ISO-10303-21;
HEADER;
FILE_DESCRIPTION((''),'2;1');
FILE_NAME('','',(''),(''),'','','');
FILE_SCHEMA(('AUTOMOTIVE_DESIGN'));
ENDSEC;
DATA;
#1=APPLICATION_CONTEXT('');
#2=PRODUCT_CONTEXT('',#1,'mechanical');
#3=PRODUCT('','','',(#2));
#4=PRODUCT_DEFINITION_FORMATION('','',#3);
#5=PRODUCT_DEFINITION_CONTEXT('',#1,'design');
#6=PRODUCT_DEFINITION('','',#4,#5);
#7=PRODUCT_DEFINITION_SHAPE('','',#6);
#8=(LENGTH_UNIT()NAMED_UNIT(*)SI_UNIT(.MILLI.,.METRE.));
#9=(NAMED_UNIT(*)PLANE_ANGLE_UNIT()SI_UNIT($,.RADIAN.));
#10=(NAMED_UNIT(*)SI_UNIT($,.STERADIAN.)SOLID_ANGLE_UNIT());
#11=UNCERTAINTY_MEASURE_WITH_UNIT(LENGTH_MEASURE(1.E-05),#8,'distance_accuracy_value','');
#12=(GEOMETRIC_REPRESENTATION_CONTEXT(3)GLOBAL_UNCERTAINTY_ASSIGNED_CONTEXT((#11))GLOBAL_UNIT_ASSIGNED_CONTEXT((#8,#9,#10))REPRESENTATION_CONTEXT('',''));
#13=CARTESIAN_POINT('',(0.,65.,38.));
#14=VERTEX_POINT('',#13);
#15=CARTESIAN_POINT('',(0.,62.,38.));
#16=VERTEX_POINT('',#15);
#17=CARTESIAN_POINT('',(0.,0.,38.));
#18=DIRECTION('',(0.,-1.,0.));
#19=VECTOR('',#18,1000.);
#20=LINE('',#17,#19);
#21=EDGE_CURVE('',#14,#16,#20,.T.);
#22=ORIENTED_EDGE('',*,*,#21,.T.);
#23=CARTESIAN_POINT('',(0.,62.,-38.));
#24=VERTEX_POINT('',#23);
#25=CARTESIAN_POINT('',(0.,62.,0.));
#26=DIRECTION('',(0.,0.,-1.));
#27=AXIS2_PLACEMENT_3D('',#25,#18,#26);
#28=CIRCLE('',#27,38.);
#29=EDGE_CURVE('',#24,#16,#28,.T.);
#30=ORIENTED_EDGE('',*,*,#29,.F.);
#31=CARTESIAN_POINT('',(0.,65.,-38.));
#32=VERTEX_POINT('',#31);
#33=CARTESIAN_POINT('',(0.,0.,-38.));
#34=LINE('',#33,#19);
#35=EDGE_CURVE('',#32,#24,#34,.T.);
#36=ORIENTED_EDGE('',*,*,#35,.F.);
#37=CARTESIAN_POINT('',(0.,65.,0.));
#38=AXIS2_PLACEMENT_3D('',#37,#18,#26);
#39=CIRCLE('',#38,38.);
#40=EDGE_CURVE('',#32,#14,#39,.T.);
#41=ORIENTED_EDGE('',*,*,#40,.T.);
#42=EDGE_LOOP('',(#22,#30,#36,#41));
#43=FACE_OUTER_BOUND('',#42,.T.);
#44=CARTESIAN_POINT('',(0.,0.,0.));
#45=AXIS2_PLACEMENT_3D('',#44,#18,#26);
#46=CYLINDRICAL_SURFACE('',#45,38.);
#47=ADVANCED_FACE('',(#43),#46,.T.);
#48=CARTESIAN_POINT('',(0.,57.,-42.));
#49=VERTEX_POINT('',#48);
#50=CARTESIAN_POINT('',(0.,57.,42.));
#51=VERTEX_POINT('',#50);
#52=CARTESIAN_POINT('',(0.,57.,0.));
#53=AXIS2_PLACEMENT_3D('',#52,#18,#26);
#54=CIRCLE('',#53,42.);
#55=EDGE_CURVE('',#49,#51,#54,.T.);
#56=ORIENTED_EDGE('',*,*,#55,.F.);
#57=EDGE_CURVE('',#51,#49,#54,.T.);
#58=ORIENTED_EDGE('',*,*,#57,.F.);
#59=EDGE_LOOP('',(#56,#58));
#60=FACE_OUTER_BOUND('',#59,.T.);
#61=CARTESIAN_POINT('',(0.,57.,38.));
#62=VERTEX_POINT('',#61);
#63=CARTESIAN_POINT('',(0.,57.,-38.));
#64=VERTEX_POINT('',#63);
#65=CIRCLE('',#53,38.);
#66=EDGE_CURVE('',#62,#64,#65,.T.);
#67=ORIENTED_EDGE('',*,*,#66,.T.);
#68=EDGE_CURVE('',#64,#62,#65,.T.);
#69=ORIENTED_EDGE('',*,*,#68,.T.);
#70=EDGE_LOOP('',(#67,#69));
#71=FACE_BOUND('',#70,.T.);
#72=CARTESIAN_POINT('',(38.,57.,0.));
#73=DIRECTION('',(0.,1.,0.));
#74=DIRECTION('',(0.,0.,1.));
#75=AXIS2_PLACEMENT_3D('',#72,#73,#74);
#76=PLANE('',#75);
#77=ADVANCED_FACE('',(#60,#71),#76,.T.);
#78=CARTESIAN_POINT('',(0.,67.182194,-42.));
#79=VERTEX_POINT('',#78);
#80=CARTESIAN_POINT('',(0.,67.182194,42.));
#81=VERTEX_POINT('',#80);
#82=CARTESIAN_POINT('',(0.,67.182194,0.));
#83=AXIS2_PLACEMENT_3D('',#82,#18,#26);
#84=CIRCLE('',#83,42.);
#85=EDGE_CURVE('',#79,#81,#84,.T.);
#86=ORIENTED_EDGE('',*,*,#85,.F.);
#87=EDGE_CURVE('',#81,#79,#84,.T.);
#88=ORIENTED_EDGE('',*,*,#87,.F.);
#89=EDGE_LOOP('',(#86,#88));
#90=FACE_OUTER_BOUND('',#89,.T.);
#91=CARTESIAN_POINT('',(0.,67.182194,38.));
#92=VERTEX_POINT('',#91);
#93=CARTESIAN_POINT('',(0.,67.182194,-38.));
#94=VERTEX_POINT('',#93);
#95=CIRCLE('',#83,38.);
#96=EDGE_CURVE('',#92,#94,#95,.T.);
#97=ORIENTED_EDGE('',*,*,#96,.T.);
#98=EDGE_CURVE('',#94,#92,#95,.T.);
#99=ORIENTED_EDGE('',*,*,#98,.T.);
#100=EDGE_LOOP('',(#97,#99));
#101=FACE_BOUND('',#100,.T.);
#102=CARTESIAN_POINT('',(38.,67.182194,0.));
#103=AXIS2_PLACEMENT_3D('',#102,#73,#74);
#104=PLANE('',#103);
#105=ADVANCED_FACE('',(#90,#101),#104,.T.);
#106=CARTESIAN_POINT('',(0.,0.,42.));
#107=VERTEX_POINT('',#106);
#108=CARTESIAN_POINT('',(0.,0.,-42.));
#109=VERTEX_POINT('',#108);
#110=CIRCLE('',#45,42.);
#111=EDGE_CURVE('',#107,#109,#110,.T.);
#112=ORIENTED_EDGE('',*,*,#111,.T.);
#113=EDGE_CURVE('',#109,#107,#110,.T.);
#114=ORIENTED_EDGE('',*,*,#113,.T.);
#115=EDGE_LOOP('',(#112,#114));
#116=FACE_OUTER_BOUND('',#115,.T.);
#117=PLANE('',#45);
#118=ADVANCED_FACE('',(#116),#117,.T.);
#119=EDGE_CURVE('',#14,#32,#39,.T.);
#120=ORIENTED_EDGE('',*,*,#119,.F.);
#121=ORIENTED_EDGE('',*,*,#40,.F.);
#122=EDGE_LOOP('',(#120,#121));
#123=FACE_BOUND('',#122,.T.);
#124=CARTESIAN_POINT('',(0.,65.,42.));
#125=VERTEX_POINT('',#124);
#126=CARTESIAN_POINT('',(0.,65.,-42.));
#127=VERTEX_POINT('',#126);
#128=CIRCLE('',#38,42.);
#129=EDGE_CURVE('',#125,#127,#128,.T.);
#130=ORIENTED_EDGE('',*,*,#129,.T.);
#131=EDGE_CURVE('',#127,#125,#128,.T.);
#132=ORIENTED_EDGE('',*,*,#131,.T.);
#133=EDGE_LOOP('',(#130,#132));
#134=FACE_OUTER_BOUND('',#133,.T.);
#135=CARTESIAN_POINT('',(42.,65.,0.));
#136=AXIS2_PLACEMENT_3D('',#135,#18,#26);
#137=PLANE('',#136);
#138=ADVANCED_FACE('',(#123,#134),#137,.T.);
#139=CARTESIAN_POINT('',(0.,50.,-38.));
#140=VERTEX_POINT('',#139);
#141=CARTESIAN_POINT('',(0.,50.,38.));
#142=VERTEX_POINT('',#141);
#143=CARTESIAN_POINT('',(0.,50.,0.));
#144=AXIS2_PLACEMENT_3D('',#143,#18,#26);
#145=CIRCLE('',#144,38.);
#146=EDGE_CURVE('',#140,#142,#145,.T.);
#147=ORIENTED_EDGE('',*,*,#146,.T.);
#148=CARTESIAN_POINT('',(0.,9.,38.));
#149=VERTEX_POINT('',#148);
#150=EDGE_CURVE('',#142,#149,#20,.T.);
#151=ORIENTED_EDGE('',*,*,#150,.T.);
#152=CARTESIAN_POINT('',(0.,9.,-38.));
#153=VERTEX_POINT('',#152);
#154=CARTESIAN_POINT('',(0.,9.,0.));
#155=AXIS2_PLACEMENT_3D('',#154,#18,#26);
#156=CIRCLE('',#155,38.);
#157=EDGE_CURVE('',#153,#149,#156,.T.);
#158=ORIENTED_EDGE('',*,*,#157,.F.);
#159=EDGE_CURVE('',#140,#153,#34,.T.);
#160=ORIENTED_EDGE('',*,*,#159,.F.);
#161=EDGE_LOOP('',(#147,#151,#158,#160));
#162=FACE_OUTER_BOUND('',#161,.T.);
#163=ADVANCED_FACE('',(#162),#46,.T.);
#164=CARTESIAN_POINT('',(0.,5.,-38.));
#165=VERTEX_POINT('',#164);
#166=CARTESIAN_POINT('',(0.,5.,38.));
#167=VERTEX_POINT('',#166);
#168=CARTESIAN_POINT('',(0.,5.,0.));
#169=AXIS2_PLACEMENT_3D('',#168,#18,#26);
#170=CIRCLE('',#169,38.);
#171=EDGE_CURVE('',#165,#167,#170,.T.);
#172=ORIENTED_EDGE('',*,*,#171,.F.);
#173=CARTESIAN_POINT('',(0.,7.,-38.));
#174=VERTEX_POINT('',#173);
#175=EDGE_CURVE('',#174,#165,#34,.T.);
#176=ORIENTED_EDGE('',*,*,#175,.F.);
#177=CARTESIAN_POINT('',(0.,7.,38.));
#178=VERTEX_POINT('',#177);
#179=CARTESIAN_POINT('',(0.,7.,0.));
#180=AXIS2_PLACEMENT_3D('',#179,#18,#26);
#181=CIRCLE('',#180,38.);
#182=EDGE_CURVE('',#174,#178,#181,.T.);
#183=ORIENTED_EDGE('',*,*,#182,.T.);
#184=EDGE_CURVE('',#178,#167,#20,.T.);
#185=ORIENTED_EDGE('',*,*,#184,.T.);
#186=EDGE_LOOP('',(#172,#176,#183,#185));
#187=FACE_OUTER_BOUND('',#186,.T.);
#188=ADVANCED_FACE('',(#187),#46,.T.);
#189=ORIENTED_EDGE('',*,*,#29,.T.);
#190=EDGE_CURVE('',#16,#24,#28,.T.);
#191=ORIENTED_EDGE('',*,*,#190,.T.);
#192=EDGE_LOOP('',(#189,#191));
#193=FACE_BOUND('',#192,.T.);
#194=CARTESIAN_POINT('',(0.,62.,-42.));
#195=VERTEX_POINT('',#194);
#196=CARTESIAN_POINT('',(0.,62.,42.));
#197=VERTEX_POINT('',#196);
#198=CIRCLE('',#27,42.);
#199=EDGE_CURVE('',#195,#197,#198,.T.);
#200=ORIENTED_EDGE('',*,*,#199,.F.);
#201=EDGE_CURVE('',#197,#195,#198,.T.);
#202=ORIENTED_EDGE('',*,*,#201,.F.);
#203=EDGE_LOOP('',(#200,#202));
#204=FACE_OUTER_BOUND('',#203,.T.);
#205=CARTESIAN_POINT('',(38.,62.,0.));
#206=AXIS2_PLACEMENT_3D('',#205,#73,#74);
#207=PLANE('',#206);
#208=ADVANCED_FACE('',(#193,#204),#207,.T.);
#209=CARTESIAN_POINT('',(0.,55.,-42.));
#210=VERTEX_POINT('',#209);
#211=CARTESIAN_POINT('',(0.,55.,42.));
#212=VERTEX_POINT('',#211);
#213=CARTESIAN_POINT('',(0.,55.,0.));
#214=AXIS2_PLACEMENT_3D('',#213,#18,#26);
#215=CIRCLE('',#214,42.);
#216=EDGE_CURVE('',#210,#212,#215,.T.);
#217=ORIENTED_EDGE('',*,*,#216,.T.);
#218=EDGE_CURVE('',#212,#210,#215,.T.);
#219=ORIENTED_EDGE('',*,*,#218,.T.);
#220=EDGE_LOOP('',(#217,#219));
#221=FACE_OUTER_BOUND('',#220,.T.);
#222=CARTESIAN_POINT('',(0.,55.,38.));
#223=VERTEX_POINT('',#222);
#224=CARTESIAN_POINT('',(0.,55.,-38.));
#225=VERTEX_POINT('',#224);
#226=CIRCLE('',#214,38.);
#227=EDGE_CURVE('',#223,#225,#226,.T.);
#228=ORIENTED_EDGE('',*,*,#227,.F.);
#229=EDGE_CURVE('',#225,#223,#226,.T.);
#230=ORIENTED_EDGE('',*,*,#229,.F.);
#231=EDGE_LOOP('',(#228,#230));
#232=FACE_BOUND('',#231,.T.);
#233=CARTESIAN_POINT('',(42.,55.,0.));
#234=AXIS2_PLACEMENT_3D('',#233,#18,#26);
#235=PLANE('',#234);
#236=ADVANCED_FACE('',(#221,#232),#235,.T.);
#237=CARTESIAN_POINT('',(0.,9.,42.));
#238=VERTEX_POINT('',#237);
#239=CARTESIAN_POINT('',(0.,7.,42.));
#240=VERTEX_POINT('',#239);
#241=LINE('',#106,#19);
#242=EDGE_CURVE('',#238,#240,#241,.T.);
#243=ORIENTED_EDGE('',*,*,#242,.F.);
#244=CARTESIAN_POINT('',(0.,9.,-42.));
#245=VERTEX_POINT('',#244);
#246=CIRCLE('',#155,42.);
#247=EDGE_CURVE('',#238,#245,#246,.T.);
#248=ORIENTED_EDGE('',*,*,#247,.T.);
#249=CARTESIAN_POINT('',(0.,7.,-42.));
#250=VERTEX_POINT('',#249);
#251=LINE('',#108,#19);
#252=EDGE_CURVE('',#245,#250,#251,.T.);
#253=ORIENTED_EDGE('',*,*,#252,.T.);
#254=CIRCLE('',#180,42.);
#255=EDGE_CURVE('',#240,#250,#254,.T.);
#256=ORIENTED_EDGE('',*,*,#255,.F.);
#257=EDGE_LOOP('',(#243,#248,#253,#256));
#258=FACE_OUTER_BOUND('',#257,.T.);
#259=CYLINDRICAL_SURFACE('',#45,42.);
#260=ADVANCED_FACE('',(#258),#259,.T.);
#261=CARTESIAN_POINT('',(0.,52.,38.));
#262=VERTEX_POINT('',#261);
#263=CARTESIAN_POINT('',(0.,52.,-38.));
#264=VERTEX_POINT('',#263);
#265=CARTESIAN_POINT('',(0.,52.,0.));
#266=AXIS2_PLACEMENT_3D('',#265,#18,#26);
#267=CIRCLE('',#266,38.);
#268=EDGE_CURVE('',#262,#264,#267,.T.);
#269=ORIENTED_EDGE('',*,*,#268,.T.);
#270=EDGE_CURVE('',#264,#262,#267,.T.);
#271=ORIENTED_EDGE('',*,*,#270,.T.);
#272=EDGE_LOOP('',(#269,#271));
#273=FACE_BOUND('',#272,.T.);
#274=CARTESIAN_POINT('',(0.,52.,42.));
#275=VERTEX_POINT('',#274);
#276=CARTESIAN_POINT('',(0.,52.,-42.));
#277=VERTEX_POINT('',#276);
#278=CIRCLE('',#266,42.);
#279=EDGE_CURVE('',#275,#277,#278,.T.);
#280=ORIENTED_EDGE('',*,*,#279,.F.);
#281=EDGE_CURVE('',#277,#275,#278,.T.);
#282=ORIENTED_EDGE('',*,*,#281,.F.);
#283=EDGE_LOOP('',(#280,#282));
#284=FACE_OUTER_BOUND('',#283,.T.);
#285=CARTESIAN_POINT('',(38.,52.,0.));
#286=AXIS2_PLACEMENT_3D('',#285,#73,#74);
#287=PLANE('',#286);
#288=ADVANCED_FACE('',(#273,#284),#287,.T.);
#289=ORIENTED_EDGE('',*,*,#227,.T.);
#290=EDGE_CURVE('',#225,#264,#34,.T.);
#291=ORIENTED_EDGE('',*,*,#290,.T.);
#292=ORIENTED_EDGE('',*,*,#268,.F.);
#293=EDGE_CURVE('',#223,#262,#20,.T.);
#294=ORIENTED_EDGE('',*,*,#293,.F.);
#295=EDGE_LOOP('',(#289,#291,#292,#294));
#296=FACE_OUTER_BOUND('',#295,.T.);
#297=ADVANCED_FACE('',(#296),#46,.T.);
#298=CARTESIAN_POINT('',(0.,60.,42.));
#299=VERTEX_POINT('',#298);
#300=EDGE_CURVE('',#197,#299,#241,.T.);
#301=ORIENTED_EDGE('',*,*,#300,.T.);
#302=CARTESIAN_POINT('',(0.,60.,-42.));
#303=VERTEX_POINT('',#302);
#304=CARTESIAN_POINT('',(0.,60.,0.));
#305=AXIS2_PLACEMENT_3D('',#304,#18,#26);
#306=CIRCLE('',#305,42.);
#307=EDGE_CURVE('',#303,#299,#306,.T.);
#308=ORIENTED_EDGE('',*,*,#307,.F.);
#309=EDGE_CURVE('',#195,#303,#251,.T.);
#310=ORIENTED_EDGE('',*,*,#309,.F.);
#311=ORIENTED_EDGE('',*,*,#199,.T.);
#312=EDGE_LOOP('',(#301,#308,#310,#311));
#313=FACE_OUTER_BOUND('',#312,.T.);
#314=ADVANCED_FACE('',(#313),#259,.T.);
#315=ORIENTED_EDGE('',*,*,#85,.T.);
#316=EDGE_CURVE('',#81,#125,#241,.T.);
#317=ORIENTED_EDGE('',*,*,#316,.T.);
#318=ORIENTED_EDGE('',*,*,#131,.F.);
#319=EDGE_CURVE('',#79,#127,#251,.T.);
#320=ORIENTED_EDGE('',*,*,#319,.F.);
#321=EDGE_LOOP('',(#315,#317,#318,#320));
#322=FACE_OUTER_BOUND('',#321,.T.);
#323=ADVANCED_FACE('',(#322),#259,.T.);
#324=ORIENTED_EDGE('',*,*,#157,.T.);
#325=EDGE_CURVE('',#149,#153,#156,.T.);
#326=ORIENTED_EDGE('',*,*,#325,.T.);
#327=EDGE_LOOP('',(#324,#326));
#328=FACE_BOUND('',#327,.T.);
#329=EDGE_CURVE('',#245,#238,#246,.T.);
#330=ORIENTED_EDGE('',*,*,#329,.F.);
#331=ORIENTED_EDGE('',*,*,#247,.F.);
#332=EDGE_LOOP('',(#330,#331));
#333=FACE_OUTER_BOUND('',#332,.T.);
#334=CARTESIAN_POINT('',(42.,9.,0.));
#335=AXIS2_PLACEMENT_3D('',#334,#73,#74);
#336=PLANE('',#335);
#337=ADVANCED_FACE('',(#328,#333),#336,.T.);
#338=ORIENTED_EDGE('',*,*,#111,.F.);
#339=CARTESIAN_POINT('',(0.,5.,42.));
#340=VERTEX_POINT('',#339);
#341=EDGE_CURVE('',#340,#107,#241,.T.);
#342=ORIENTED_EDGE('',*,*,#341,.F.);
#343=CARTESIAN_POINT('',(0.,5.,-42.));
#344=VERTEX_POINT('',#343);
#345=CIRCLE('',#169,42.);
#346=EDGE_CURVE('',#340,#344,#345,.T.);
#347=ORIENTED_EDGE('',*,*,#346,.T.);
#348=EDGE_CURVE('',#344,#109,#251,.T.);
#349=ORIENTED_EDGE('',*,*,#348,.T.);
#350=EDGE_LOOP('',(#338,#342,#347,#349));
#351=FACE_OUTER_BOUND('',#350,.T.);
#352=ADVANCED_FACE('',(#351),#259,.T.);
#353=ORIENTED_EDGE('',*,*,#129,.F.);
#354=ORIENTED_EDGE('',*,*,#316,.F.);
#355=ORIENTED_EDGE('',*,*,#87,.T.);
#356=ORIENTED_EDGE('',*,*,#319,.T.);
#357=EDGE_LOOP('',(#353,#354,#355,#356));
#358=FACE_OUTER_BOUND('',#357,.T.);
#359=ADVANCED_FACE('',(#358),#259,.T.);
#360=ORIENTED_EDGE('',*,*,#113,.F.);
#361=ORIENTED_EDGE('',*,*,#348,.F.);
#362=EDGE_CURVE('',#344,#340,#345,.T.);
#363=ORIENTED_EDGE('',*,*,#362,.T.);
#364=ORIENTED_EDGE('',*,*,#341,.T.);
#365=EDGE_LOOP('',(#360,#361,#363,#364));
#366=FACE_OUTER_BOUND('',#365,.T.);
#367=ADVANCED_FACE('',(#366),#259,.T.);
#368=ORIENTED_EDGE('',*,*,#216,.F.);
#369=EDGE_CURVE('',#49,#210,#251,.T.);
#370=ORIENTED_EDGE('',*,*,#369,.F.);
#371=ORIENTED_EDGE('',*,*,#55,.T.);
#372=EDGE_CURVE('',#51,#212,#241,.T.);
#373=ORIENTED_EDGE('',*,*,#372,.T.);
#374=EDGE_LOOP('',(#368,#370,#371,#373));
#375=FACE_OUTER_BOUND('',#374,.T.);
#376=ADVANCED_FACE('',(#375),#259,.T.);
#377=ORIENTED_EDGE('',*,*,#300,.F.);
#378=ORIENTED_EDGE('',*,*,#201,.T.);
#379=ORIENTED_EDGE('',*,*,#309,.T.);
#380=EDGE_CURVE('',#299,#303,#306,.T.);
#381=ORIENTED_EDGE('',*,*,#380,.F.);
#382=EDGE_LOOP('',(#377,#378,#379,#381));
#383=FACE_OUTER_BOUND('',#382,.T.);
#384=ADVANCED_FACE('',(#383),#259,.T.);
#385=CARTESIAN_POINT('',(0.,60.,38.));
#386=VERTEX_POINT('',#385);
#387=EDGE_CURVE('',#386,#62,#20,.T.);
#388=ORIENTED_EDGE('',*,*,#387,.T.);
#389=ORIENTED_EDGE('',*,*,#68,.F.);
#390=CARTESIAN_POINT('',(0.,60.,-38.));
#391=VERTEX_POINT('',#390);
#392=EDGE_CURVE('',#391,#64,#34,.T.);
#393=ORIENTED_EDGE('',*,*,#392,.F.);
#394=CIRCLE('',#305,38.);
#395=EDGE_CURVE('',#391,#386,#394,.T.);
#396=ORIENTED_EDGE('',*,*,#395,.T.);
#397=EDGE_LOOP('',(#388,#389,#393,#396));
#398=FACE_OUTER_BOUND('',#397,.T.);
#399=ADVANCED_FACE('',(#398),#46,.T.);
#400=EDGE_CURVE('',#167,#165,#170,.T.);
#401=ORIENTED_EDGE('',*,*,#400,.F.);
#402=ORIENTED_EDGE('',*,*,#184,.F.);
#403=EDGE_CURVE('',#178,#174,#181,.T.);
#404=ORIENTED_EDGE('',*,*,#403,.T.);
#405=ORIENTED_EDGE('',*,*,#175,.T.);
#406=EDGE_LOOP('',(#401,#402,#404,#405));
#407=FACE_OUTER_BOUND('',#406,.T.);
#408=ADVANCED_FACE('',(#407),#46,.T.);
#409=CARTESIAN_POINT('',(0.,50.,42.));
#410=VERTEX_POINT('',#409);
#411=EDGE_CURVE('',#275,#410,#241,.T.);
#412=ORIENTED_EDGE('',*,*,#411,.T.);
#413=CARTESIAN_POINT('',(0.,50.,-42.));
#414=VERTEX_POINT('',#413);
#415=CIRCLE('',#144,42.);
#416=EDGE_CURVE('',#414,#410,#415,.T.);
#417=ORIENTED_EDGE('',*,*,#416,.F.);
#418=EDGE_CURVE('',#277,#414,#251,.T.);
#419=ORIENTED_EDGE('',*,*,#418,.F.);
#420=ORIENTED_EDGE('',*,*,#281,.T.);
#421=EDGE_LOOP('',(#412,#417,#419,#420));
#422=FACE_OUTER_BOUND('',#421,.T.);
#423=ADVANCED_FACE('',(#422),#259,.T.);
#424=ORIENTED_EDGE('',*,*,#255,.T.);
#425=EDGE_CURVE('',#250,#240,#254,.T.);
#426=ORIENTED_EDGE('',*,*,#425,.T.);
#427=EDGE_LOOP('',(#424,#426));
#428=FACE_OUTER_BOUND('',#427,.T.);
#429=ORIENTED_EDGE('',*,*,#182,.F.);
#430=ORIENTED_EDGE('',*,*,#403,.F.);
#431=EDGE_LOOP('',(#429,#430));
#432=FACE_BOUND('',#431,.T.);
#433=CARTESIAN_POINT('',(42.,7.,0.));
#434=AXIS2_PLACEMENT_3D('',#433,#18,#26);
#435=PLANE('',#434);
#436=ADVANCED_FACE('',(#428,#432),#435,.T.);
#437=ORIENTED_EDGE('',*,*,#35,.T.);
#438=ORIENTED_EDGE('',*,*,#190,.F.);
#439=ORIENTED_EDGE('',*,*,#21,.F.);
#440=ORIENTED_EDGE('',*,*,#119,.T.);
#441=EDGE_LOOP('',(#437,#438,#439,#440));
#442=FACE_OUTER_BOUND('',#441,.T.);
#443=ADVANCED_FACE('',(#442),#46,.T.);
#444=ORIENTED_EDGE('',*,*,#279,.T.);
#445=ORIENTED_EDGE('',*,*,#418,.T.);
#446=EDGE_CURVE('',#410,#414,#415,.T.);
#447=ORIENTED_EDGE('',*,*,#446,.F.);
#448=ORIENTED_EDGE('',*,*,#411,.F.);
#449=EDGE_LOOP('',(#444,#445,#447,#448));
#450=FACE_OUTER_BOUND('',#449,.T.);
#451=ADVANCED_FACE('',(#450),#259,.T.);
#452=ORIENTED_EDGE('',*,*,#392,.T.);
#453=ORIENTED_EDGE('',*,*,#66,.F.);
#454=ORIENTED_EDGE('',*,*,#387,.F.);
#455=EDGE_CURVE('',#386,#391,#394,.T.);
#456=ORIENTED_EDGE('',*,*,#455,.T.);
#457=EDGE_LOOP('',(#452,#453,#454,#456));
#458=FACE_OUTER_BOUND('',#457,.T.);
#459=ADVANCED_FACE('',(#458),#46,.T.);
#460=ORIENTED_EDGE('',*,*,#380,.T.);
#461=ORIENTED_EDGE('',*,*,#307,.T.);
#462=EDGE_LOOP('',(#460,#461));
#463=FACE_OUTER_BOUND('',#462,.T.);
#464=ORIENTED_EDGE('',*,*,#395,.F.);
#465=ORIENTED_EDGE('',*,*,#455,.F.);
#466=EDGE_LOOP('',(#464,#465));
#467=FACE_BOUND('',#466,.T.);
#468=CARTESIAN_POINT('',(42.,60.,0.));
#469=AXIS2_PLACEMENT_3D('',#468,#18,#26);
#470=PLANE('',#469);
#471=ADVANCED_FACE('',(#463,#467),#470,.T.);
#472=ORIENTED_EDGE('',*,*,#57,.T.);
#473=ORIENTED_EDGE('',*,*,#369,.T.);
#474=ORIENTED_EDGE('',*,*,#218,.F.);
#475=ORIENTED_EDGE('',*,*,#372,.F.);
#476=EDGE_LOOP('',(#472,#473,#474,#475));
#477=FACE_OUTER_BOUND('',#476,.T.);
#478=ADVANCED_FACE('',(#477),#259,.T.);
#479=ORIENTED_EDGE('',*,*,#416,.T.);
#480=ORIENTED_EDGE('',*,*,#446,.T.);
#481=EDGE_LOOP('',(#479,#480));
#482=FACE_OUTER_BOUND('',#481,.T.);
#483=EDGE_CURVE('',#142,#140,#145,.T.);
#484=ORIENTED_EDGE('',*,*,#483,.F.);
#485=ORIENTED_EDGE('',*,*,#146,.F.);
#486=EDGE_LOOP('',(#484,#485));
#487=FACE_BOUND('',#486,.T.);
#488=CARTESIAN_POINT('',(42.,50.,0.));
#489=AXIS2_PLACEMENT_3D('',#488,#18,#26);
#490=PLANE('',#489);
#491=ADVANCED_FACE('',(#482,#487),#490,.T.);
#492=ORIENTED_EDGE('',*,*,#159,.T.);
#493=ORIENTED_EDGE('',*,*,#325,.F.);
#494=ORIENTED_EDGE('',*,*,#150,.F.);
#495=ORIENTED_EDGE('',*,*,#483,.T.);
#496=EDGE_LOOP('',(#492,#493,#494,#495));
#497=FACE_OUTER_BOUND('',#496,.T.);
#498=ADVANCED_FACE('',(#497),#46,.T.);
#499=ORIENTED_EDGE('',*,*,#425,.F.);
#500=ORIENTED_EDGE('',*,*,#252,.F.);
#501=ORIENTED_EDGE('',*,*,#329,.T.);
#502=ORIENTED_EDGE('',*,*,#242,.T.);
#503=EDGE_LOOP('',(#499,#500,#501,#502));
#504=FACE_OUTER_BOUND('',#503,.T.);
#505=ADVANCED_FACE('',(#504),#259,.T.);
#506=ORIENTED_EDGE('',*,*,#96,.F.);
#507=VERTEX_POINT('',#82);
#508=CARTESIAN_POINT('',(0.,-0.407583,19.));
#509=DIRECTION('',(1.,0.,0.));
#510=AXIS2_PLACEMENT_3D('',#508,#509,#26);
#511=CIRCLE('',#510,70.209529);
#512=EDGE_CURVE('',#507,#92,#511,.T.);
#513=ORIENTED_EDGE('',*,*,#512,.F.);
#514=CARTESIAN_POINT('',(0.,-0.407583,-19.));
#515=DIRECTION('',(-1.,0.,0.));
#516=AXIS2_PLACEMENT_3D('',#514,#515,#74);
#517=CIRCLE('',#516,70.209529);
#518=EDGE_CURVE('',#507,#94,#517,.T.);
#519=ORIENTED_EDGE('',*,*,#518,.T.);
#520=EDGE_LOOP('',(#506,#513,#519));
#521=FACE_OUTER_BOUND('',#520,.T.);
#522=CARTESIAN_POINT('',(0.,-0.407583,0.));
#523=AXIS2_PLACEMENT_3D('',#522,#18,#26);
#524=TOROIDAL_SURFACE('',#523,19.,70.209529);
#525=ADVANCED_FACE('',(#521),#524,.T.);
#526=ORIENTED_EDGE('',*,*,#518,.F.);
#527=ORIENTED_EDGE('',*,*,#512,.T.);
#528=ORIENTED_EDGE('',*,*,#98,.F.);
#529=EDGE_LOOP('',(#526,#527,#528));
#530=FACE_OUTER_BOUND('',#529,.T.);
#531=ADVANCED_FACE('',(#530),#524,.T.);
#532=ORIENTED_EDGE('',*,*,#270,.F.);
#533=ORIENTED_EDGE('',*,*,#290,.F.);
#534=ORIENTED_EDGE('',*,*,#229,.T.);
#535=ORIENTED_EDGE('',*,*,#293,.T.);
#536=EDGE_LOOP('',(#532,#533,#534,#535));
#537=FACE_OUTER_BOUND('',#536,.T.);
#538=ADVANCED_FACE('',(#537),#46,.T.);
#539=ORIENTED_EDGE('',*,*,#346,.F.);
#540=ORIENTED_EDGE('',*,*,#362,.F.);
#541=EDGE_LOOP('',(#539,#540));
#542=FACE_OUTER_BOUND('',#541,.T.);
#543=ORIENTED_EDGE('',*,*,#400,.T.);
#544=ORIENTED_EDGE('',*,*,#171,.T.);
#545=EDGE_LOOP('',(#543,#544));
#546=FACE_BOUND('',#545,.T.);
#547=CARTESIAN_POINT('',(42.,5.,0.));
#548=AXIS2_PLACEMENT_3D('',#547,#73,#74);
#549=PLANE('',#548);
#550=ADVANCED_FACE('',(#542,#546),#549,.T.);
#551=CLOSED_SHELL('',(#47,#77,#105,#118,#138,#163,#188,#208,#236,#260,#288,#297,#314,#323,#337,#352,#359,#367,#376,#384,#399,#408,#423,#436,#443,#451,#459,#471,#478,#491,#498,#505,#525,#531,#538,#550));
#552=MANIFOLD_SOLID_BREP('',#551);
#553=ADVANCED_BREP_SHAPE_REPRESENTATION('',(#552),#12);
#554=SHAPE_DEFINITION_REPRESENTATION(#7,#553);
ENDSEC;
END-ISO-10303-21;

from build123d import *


with BuildPart() as part:
    # Piston Profile Sketch → Piston Body Revolve (revolve)
    with BuildSketch(Plane.XY, mode=Mode.PRIVATE) as piston_body_revolve_sk:
        with BuildLine():
            Line((0, 0), (37, 0))
            Line((37, 0), (42, 0))
            Line((42, 0), (42, 5))
            Line((42, 5), (38, 5))
            Line((38, 5), (38, 7))
            Line((38, 7), (42, 7))
            Line((42, 7), (42, 9))
            Line((42, 9), (38, 9))
            Line((38, 9), (38, 50))
            Line((38, 50), (42, 50))
            Line((42, 50), (42, 52))
            Line((42, 52), (38, 52))
            Line((38, 52), (38, 55))
            Line((38, 55), (42, 55))
            Line((42, 55), (42, 57))
            Line((42, 57), (38, 57))
            Line((38, 57), (38, 60))
            Line((38, 60), (42, 60))
            Line((42, 60), (42, 62))
            Line((42, 62), (38, 62))
            Line((38, 62), (38, 65))
            Line((38, 65), (42, 65))
            Line((42, 65), (42, 67.182193635))
            Line((42, 67.182193635), (38, 67.182193635))
            ThreePointArc((38, 67.182193635), (19, 69.801945586), (0, 67.182193635))
            Line((0, 67.182193635), (0, 0))
        make_face()
    revolve(piston_body_revolve_sk.sketch.rotate(Axis((0, 0, 0), (0, 1, 0)), 90), axis=Axis((0, 0, 0), (0, 1, 0)))


solid = part.part
